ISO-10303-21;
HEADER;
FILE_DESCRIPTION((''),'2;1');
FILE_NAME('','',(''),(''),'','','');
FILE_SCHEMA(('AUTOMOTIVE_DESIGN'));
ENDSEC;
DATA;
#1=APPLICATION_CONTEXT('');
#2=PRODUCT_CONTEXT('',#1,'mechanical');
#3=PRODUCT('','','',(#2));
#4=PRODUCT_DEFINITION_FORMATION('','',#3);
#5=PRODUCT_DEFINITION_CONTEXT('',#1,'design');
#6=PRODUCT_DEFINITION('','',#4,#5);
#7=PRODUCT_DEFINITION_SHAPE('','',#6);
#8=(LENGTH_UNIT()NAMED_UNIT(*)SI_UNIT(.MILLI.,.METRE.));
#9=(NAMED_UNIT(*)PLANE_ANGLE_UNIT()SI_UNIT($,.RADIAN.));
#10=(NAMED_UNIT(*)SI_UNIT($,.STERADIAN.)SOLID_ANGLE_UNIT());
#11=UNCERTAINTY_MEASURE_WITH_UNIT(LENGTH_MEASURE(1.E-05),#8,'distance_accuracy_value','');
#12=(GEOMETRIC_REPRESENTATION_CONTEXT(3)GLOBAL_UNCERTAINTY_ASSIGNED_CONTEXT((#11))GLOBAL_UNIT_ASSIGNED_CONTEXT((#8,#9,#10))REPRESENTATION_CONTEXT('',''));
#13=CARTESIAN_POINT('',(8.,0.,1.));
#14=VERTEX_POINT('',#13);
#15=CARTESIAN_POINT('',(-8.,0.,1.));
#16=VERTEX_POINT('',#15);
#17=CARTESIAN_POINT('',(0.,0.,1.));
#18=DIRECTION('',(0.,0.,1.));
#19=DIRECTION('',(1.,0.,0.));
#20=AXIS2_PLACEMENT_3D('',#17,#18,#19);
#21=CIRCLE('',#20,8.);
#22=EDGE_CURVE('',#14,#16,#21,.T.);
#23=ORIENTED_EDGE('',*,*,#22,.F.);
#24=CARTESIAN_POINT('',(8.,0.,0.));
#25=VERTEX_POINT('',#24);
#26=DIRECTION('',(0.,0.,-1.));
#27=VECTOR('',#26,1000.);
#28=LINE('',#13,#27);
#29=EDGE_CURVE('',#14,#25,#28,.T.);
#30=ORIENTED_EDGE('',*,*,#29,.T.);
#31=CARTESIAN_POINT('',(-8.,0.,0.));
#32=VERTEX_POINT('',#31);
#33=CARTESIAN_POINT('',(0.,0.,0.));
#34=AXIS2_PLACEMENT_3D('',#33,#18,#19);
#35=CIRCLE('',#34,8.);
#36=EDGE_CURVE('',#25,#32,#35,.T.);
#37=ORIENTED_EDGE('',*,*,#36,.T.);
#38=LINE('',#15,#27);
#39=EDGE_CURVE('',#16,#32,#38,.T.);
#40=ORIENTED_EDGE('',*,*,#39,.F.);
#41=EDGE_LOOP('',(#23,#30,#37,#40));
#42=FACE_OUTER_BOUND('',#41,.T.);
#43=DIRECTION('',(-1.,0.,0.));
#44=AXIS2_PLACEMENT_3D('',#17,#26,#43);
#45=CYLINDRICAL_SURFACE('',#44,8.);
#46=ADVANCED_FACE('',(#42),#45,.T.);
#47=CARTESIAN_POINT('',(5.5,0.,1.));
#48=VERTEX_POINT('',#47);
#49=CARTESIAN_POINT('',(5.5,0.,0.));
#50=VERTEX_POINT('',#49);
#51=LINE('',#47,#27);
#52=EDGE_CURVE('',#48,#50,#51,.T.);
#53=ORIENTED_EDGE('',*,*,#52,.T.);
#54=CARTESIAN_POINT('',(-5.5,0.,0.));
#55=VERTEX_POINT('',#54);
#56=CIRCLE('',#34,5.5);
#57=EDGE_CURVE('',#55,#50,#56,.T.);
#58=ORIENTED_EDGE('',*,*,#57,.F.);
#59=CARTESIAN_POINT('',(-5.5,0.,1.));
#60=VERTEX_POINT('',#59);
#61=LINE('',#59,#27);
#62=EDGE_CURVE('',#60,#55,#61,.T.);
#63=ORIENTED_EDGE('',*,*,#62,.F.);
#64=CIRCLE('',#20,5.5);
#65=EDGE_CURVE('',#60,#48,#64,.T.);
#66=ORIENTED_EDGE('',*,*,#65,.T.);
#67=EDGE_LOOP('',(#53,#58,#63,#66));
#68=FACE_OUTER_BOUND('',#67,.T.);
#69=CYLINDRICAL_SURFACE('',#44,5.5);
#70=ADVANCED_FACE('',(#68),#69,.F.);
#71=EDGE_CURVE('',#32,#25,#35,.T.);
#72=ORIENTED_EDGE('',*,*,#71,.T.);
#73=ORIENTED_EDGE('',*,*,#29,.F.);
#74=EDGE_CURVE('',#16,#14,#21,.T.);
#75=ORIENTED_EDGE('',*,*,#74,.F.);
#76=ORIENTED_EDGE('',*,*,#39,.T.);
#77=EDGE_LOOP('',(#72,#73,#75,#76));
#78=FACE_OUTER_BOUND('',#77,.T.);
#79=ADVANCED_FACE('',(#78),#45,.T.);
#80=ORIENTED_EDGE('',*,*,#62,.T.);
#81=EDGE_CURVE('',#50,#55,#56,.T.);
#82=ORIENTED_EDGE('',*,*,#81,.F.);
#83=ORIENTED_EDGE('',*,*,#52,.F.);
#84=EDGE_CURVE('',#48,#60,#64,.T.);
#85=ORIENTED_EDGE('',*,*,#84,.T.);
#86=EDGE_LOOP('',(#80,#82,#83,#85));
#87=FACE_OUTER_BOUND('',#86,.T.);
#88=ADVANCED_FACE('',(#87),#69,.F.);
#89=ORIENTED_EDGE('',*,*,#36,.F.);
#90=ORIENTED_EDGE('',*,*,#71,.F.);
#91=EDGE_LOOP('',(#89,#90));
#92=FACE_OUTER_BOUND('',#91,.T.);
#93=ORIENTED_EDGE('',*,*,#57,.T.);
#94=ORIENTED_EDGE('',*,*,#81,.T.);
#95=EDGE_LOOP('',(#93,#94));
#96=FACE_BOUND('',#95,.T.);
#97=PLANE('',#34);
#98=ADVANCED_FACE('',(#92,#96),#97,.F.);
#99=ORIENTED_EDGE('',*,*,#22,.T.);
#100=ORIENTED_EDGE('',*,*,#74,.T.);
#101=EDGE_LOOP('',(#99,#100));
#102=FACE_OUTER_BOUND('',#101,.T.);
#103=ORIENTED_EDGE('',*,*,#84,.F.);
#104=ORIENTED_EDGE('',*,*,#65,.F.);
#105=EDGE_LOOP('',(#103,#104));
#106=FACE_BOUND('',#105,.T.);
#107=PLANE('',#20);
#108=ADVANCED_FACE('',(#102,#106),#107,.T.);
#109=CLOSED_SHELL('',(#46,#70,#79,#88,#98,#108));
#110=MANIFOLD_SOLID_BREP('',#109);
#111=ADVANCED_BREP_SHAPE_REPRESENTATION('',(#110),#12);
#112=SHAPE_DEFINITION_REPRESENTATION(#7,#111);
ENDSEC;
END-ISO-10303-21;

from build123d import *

# Parameters (mm, degrees)
SKETCH_1_R      = 8
SKETCH_1_R_2    = 5.5
EXTRUDE_1_DEPTH = 1


with BuildPart() as part:
    # 草图1 → 凸台-拉伸1 (new body)
    with BuildSketch(Plane.XY):
        Circle(SKETCH_1_R)
        Circle(SKETCH_1_R_2, mode=Mode.SUBTRACT)
    extrude(amount=EXTRUDE_1_DEPTH)


solid = part.part
